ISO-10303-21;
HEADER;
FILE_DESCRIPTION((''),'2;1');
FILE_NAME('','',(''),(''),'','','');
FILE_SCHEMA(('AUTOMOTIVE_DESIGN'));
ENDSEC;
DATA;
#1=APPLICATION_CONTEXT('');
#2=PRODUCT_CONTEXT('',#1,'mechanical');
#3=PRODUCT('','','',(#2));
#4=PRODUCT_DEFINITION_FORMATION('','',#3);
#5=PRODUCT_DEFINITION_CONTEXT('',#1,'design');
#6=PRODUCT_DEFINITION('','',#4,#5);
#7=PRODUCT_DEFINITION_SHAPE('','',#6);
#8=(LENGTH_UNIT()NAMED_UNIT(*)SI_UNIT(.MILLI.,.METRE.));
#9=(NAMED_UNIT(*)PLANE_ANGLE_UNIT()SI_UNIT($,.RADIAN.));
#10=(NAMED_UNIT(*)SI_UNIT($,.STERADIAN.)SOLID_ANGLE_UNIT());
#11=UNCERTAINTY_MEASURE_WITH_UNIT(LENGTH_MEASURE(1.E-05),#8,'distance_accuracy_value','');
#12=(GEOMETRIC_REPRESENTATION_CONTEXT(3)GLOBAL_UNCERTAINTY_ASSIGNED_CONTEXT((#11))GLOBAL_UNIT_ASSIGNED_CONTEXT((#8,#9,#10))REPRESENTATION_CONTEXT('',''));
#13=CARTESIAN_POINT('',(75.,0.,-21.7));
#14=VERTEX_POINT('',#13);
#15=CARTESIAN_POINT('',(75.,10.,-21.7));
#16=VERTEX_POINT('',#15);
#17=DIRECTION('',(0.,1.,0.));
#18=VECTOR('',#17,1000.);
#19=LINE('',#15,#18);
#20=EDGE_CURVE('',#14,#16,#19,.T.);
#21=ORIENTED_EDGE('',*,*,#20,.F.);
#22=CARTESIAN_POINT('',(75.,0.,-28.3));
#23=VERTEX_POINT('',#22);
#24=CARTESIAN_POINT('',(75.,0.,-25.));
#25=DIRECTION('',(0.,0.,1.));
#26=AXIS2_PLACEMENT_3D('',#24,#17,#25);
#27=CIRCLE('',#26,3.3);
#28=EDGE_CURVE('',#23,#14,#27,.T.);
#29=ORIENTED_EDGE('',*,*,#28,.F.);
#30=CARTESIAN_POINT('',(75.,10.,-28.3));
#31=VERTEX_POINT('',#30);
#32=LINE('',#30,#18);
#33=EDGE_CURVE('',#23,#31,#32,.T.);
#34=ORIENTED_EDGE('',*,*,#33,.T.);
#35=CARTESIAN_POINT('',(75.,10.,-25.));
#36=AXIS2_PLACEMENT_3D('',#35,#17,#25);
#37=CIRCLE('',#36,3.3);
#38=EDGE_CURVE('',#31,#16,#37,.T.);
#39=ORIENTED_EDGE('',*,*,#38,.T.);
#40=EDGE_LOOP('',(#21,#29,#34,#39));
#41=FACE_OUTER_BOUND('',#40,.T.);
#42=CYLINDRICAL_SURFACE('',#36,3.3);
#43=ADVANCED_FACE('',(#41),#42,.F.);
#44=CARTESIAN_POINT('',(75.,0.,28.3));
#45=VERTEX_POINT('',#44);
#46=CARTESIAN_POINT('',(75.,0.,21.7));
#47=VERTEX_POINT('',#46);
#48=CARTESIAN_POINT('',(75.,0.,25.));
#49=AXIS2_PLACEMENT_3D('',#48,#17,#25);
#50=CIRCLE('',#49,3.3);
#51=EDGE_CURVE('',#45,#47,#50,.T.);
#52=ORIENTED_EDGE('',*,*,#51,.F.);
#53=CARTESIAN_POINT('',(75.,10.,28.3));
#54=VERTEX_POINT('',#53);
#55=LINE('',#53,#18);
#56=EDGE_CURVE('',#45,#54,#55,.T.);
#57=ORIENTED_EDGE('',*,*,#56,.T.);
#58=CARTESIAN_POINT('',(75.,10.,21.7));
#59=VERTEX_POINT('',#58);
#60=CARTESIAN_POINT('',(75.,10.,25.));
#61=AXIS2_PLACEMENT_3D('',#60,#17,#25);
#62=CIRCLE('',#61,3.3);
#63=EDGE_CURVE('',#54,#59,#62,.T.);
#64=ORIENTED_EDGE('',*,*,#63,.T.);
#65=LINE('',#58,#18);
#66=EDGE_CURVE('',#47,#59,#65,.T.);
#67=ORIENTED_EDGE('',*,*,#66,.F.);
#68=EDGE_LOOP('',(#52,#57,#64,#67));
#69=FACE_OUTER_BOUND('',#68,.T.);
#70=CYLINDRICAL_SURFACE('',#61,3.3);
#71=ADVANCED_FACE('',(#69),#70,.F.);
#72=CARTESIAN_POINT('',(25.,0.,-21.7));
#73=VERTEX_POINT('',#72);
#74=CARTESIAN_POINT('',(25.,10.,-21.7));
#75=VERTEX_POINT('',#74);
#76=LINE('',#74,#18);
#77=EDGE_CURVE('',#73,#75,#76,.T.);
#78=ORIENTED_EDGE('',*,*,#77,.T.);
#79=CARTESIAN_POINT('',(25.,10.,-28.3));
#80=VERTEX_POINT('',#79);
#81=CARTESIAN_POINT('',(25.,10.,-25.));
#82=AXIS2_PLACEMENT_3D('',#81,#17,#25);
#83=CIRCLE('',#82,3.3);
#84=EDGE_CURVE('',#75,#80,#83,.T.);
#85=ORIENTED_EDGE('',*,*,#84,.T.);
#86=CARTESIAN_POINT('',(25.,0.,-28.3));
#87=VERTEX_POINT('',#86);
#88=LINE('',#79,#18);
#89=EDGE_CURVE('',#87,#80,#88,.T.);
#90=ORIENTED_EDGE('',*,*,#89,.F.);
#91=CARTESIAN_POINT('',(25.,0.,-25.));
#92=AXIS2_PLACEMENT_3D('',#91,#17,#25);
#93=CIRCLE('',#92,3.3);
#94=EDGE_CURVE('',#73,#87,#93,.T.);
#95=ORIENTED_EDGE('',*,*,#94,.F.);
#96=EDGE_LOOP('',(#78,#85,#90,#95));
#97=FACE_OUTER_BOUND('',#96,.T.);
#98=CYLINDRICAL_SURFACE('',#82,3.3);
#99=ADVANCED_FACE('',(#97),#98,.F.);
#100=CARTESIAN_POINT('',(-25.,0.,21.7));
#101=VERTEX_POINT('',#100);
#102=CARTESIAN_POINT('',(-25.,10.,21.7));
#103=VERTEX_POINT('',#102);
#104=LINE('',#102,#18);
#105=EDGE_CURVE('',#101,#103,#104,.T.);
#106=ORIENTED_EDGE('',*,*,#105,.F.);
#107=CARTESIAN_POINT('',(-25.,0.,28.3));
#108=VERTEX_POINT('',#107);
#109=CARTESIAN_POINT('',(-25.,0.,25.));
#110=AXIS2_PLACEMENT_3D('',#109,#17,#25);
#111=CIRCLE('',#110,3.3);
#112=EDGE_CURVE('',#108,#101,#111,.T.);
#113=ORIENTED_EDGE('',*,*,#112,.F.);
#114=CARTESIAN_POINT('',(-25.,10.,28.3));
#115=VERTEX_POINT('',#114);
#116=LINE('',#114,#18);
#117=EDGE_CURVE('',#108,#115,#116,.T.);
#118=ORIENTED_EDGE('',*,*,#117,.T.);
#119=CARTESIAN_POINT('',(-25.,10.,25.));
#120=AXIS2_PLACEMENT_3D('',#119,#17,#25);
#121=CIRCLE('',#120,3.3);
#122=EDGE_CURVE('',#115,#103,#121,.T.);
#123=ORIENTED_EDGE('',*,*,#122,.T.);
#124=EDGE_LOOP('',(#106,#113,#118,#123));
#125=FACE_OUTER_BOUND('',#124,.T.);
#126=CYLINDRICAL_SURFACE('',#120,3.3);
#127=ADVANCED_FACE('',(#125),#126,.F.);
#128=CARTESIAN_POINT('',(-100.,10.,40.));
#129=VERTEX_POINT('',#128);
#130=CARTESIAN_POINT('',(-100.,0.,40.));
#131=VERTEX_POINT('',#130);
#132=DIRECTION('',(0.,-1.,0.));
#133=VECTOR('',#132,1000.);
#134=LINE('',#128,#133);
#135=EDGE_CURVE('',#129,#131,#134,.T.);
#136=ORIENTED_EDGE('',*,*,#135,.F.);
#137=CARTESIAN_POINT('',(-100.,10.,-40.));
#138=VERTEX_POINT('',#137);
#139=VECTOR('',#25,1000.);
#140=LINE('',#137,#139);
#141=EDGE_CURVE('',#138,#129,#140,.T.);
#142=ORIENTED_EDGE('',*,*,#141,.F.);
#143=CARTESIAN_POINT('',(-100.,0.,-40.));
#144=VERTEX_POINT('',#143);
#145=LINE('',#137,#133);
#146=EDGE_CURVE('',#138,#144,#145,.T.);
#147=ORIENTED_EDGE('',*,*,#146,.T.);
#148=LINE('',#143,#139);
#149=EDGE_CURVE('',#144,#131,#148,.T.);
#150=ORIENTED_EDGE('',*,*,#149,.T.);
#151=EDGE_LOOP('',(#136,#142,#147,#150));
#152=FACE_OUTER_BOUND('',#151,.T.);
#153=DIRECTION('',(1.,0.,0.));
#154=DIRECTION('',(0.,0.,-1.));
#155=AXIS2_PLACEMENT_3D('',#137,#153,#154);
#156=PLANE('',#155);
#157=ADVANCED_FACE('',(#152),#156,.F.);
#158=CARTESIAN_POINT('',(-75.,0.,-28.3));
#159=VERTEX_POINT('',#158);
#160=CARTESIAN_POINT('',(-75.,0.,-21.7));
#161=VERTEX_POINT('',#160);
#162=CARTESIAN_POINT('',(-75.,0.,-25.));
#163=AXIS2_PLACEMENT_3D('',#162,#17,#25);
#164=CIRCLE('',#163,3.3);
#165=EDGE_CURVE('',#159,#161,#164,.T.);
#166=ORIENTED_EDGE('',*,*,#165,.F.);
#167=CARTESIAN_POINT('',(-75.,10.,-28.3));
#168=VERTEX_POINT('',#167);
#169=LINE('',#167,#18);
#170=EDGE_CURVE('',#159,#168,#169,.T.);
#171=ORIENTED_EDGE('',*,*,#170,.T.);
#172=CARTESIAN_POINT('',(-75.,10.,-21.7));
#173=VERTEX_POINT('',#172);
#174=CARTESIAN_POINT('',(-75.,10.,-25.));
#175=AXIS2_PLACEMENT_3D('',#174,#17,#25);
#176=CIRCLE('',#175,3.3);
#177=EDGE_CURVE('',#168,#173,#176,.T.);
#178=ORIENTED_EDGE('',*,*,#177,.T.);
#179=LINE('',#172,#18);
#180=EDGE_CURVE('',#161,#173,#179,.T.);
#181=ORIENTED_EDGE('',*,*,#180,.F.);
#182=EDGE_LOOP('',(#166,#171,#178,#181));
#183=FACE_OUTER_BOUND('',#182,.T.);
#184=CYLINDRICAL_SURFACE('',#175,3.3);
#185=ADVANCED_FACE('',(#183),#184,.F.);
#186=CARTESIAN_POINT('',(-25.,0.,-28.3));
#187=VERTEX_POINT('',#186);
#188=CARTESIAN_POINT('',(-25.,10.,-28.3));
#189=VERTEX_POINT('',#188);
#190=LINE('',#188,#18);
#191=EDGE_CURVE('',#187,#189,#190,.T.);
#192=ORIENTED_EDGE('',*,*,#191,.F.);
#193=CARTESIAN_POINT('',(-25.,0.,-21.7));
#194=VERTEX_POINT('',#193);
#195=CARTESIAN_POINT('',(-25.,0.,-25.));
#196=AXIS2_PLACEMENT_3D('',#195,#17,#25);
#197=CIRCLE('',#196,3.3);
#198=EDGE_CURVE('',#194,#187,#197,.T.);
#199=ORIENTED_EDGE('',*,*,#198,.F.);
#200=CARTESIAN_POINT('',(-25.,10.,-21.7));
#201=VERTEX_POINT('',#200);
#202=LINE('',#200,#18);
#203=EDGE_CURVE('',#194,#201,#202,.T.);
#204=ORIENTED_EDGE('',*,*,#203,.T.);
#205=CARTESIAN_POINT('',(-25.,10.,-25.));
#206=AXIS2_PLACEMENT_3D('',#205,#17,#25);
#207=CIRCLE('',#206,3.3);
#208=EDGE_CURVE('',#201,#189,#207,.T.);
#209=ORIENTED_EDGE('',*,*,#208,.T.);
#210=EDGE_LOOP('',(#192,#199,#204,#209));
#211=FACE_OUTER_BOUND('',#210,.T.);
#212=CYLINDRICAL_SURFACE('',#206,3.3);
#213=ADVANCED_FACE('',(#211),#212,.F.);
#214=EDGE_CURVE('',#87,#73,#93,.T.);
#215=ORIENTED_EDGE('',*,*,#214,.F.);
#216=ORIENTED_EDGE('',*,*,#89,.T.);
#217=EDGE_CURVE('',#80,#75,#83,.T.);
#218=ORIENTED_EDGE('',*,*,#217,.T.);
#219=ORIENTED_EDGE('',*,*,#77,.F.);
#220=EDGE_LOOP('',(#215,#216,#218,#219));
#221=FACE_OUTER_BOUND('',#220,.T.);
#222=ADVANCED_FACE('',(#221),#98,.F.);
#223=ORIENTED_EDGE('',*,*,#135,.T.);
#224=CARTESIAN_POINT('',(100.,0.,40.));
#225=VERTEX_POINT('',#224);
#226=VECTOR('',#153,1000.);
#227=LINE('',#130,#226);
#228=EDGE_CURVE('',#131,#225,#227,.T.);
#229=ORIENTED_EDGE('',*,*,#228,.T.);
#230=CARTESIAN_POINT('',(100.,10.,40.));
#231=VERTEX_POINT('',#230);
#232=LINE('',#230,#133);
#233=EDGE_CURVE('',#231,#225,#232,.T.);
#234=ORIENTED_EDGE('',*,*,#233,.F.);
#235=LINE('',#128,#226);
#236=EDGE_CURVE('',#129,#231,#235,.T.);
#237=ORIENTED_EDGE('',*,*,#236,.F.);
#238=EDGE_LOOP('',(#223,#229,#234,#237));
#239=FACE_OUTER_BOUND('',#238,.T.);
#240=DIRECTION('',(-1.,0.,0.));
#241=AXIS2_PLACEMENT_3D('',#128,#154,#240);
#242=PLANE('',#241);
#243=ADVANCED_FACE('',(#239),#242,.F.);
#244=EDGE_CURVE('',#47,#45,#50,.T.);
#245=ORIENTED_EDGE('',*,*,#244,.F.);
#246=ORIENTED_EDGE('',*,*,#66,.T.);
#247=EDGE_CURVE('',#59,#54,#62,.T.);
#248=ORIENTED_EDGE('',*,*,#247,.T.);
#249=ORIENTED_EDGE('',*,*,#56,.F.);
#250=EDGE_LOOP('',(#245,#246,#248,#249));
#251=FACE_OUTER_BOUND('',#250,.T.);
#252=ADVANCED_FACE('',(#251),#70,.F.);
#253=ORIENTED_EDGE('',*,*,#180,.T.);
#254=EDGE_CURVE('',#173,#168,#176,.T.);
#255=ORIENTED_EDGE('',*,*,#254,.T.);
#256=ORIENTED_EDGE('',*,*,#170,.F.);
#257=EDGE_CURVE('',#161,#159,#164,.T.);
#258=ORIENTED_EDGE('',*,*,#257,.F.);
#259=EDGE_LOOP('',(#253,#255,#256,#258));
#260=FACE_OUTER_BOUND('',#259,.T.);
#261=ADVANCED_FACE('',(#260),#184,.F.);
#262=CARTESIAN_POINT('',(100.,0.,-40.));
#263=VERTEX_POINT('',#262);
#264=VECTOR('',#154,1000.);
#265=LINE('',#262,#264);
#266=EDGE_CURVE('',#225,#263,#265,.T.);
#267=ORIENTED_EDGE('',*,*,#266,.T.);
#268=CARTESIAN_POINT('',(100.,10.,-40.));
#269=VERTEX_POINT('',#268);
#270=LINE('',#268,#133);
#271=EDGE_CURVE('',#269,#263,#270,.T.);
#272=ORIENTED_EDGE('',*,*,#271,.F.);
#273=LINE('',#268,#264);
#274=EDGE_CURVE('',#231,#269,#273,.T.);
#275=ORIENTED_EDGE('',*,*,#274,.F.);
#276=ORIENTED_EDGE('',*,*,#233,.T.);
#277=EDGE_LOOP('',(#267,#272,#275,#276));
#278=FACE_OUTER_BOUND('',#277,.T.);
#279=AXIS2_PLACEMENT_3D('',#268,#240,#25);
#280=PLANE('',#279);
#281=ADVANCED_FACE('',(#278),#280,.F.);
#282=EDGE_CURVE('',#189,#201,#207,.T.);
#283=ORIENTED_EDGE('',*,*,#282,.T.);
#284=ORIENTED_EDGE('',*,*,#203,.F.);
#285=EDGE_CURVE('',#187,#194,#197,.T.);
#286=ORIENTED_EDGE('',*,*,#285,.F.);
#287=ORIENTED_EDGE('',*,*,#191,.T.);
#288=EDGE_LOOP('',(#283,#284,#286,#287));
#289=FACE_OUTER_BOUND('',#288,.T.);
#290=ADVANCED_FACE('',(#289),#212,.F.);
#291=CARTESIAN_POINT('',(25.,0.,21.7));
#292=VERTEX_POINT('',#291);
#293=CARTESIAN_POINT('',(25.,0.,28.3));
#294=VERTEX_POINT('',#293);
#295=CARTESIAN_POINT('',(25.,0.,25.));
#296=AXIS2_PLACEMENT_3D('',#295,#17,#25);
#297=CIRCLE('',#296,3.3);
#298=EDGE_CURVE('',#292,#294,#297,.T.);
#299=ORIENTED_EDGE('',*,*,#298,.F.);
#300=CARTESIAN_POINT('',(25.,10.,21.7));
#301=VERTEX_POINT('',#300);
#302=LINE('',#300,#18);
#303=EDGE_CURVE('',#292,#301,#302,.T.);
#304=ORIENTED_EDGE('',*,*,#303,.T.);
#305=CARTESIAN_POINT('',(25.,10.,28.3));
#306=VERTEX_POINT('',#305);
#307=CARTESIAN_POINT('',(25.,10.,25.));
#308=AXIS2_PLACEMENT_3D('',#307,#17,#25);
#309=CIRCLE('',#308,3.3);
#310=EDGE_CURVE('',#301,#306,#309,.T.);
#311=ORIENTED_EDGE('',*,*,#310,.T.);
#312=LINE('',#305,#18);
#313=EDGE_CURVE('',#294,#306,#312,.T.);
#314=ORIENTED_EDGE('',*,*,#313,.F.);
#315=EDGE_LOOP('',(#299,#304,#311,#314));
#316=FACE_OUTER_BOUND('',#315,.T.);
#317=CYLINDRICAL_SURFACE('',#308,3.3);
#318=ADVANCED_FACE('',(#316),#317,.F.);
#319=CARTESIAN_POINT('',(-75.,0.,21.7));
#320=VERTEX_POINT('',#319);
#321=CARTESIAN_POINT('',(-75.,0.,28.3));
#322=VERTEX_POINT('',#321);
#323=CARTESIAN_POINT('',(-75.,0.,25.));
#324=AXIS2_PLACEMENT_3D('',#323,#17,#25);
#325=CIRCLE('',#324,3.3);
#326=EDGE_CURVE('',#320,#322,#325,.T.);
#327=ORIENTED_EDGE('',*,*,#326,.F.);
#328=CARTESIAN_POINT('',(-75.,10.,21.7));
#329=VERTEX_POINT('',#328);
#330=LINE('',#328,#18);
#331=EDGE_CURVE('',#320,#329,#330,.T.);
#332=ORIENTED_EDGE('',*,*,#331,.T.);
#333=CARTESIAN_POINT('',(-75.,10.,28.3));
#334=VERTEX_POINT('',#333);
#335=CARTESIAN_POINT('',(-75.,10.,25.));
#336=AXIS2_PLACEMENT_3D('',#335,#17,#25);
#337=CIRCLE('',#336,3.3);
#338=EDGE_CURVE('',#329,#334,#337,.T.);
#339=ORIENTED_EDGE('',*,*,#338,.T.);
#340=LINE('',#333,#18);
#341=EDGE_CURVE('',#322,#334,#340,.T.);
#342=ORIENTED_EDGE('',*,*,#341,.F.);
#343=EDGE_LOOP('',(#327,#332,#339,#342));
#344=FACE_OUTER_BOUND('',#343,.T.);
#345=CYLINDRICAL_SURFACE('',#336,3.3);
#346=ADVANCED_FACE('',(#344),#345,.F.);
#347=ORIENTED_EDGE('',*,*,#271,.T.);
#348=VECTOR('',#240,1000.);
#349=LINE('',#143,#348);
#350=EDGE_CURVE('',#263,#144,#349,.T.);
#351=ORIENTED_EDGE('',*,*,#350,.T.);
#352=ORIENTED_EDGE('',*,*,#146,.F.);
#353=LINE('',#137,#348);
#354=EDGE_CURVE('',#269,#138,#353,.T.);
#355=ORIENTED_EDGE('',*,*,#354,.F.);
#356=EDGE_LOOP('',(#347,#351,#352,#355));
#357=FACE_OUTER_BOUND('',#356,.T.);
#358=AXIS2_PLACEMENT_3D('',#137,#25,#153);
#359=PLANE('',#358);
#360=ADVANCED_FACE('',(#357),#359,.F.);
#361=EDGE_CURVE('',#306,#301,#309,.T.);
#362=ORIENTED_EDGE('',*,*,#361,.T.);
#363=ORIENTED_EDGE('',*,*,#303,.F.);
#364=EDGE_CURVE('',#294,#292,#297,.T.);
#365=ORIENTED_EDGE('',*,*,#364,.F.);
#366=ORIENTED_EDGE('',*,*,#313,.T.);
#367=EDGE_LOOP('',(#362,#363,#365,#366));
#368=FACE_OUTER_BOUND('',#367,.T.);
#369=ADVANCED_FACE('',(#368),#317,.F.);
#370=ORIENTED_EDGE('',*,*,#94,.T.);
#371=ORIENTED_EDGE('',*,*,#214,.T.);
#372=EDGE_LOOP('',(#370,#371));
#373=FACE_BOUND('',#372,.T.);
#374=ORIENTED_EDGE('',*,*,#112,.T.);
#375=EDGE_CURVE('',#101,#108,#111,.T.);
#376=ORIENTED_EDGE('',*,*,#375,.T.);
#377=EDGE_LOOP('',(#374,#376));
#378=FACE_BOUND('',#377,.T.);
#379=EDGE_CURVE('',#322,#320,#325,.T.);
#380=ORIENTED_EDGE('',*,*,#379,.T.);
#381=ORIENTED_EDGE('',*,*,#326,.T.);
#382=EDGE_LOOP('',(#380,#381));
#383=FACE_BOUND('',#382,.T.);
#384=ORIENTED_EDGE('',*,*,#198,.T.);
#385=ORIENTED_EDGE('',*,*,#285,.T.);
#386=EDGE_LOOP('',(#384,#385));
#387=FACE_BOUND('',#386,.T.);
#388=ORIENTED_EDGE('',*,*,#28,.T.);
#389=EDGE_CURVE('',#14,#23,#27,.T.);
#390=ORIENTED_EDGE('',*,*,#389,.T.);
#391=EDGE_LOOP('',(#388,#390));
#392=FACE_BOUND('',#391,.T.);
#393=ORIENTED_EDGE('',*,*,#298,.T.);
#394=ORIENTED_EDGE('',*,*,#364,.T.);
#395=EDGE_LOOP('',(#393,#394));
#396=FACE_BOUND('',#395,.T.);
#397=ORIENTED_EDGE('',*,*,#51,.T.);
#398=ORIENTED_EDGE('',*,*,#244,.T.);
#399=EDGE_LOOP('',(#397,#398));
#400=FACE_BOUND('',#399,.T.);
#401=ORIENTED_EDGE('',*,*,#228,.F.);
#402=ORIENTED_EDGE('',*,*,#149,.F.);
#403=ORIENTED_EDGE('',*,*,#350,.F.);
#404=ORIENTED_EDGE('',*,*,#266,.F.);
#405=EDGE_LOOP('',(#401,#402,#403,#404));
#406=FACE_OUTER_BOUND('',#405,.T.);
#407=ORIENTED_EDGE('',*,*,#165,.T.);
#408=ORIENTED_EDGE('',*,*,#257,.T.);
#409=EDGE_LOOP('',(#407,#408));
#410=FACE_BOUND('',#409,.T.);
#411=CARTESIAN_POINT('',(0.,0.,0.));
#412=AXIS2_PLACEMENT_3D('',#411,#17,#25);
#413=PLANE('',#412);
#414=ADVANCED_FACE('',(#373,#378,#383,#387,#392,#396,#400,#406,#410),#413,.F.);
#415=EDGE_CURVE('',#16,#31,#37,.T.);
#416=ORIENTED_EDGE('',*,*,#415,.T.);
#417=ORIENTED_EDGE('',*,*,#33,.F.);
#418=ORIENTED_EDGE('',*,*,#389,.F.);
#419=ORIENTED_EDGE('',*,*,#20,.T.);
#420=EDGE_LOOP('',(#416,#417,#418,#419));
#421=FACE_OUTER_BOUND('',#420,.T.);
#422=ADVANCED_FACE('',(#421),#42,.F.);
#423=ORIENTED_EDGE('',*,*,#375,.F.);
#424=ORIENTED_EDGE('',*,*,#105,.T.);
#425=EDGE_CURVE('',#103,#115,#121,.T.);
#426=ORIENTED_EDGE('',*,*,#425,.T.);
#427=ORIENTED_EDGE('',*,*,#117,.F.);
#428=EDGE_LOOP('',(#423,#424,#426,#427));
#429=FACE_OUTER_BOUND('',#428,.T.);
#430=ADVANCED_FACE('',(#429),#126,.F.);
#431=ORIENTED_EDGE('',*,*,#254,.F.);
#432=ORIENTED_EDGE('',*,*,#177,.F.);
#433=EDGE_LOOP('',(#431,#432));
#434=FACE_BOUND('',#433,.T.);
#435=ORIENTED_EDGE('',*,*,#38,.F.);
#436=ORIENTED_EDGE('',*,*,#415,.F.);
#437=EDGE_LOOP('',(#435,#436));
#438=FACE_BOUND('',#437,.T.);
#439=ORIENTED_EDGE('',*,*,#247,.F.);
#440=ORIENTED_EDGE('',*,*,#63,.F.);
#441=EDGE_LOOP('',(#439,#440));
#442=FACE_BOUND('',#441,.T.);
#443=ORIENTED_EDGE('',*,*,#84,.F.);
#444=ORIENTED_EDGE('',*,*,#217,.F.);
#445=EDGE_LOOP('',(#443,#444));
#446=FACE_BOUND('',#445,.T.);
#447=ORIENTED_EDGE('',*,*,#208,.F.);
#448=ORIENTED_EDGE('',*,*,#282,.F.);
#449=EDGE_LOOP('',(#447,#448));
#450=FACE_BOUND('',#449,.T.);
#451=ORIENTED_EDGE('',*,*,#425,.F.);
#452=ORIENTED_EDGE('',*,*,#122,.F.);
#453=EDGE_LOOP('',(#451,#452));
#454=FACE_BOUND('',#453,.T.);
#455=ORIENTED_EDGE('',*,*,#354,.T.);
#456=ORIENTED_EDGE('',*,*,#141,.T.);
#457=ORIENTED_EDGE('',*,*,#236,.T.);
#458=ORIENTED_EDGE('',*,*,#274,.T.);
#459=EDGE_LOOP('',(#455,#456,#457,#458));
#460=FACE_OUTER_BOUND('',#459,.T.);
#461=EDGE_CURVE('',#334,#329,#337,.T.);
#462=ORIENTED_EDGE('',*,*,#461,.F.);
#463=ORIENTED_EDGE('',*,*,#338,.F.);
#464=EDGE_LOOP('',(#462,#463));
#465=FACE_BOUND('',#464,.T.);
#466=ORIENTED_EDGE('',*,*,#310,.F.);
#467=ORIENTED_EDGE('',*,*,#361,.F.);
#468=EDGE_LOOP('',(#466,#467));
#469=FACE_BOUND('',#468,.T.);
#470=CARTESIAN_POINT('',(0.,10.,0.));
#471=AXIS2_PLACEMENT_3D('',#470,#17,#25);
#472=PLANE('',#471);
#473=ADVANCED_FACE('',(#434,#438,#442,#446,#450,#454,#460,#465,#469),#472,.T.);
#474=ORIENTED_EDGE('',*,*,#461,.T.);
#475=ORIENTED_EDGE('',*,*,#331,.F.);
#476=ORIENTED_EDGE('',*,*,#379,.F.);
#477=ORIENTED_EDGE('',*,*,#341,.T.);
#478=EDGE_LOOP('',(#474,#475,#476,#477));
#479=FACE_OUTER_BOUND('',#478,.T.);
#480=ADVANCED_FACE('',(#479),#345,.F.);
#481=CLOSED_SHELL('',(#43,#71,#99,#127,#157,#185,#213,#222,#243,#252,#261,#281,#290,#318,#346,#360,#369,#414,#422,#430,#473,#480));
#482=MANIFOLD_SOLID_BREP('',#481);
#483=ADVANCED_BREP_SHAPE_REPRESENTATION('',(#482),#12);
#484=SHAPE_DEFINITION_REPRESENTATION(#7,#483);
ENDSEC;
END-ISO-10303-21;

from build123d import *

# Parameters (mm, degrees)
SKETCH1_W                  = 200
SKETCH1_H                  = 80
BOSS_EXTRUDE1_DEPTH        = 10
F_6_6_6_6_DIAMETER_HOLE1_D = 6.6


with BuildPart() as part:
    # Sketch1 → Boss-Extrude1 (new body)
    with BuildSketch(Plane(origin=(0, 0, 0), x_dir=(1, 0, 0), z_dir=(0, 1, 0))):
        Rectangle(SKETCH1_W, SKETCH1_H)
    extrude(amount=BOSS_EXTRUDE1_DEPTH)

    # Ø6.6 (6.6) Diameter Hole1 (through all)
    with Locations(Plane(origin=(0, 10, 0), x_dir=(1, 0, 0), z_dir=(0, 1, 0))):
        with Locations((-25, 25), (25, 25), (-25, -25), (25, -25), (-75, 25), (75, 25), (75, -25), (-75, -25)):
            Hole(F_6_6_6_6_DIAMETER_HOLE1_D / 2)


solid = part.part
